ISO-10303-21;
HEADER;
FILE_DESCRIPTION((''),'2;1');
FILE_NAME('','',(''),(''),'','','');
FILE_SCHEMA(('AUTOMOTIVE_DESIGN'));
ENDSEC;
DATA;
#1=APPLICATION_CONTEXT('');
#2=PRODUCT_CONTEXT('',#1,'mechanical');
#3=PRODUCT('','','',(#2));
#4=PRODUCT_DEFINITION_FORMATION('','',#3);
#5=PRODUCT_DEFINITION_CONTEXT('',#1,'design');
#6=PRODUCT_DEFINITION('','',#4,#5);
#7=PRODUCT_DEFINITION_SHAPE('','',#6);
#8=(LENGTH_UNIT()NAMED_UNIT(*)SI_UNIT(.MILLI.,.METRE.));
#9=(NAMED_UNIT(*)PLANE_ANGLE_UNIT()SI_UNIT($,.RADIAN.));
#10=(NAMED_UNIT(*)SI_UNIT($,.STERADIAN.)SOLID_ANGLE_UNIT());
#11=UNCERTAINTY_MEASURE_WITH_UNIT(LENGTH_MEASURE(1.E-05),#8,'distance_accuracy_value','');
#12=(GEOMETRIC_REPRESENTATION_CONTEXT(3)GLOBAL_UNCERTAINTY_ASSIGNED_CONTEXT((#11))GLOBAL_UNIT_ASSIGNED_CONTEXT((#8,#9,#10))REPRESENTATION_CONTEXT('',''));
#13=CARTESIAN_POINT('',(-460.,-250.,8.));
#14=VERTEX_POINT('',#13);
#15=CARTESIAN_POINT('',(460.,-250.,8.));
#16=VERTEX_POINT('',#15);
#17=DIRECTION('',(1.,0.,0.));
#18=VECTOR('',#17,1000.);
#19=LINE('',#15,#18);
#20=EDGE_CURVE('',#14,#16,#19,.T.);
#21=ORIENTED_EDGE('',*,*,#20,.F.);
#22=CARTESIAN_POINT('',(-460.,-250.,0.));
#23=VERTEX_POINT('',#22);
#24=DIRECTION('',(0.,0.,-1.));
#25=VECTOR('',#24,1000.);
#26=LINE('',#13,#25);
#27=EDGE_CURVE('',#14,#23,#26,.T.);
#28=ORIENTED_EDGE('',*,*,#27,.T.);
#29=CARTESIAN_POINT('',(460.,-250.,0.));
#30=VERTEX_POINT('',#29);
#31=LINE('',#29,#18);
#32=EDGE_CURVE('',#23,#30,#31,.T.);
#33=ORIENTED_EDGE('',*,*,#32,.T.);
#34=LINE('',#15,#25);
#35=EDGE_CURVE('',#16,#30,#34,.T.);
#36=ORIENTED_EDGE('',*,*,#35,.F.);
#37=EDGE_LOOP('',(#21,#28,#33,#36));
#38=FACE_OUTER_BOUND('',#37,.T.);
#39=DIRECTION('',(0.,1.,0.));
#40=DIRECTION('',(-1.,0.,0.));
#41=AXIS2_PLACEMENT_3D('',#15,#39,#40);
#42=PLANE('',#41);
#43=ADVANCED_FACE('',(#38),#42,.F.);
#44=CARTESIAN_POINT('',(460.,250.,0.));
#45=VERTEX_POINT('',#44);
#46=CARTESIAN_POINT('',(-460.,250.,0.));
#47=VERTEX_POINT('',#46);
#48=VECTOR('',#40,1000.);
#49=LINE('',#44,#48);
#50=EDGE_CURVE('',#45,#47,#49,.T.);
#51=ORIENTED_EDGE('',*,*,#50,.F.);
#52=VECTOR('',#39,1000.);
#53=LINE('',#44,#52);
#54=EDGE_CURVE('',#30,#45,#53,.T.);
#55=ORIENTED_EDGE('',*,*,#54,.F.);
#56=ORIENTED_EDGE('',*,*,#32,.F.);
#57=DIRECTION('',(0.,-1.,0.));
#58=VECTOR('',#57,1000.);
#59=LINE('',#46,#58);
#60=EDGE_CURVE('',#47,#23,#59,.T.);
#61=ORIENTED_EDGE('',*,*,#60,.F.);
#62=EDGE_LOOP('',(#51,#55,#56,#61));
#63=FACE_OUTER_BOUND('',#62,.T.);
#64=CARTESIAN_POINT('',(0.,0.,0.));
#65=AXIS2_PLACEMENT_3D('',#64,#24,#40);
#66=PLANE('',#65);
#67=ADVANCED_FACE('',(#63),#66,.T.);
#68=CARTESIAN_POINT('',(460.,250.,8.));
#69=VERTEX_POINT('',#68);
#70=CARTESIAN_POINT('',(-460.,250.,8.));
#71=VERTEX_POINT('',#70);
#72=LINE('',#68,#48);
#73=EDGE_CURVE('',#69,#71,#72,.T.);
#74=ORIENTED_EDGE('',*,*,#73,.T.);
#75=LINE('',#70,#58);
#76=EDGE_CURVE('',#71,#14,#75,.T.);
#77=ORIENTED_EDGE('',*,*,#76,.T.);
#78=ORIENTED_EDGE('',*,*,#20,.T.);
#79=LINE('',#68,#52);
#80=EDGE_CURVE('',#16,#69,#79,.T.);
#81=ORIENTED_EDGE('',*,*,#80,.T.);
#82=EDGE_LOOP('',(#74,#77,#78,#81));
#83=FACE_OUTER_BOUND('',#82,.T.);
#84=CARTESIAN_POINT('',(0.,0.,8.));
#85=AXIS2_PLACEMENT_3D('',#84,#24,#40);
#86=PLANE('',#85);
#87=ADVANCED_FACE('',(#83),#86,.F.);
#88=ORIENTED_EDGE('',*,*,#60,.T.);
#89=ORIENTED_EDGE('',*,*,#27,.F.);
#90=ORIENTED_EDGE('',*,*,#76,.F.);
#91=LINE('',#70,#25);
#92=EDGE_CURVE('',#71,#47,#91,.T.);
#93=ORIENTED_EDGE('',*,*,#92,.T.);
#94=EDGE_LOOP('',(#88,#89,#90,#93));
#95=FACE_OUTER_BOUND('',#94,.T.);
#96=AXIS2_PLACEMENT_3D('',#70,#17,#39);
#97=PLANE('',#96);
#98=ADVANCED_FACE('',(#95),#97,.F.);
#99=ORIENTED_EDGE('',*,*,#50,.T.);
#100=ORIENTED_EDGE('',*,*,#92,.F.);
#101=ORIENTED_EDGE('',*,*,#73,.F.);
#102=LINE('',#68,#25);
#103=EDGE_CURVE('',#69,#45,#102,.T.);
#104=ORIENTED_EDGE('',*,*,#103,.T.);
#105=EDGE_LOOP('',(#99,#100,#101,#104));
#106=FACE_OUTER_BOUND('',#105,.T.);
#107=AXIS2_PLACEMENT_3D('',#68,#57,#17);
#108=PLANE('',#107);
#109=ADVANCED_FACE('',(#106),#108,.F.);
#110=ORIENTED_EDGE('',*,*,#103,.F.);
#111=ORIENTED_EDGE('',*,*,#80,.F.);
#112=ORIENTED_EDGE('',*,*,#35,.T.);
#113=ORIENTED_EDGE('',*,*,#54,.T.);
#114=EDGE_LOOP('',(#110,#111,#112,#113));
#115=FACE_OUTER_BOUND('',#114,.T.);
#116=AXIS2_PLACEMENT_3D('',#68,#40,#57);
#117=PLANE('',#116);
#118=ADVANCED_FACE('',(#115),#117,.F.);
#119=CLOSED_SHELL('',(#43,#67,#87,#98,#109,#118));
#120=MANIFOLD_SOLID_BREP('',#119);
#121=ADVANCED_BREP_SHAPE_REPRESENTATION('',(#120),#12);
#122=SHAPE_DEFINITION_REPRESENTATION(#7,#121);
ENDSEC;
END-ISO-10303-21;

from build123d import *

# Parameters (mm, degrees)
SKETCH1_W           = 920
SKETCH1_H           = 500
BOSS_EXTRUDE1_DEPTH = 8


with BuildPart() as part:
    # Sketch1 → Boss-Extrude1 (new body)
    with BuildSketch(Plane.XY):
        Rectangle(SKETCH1_W, SKETCH1_H)
    extrude(amount=BOSS_EXTRUDE1_DEPTH)


solid = part.part
